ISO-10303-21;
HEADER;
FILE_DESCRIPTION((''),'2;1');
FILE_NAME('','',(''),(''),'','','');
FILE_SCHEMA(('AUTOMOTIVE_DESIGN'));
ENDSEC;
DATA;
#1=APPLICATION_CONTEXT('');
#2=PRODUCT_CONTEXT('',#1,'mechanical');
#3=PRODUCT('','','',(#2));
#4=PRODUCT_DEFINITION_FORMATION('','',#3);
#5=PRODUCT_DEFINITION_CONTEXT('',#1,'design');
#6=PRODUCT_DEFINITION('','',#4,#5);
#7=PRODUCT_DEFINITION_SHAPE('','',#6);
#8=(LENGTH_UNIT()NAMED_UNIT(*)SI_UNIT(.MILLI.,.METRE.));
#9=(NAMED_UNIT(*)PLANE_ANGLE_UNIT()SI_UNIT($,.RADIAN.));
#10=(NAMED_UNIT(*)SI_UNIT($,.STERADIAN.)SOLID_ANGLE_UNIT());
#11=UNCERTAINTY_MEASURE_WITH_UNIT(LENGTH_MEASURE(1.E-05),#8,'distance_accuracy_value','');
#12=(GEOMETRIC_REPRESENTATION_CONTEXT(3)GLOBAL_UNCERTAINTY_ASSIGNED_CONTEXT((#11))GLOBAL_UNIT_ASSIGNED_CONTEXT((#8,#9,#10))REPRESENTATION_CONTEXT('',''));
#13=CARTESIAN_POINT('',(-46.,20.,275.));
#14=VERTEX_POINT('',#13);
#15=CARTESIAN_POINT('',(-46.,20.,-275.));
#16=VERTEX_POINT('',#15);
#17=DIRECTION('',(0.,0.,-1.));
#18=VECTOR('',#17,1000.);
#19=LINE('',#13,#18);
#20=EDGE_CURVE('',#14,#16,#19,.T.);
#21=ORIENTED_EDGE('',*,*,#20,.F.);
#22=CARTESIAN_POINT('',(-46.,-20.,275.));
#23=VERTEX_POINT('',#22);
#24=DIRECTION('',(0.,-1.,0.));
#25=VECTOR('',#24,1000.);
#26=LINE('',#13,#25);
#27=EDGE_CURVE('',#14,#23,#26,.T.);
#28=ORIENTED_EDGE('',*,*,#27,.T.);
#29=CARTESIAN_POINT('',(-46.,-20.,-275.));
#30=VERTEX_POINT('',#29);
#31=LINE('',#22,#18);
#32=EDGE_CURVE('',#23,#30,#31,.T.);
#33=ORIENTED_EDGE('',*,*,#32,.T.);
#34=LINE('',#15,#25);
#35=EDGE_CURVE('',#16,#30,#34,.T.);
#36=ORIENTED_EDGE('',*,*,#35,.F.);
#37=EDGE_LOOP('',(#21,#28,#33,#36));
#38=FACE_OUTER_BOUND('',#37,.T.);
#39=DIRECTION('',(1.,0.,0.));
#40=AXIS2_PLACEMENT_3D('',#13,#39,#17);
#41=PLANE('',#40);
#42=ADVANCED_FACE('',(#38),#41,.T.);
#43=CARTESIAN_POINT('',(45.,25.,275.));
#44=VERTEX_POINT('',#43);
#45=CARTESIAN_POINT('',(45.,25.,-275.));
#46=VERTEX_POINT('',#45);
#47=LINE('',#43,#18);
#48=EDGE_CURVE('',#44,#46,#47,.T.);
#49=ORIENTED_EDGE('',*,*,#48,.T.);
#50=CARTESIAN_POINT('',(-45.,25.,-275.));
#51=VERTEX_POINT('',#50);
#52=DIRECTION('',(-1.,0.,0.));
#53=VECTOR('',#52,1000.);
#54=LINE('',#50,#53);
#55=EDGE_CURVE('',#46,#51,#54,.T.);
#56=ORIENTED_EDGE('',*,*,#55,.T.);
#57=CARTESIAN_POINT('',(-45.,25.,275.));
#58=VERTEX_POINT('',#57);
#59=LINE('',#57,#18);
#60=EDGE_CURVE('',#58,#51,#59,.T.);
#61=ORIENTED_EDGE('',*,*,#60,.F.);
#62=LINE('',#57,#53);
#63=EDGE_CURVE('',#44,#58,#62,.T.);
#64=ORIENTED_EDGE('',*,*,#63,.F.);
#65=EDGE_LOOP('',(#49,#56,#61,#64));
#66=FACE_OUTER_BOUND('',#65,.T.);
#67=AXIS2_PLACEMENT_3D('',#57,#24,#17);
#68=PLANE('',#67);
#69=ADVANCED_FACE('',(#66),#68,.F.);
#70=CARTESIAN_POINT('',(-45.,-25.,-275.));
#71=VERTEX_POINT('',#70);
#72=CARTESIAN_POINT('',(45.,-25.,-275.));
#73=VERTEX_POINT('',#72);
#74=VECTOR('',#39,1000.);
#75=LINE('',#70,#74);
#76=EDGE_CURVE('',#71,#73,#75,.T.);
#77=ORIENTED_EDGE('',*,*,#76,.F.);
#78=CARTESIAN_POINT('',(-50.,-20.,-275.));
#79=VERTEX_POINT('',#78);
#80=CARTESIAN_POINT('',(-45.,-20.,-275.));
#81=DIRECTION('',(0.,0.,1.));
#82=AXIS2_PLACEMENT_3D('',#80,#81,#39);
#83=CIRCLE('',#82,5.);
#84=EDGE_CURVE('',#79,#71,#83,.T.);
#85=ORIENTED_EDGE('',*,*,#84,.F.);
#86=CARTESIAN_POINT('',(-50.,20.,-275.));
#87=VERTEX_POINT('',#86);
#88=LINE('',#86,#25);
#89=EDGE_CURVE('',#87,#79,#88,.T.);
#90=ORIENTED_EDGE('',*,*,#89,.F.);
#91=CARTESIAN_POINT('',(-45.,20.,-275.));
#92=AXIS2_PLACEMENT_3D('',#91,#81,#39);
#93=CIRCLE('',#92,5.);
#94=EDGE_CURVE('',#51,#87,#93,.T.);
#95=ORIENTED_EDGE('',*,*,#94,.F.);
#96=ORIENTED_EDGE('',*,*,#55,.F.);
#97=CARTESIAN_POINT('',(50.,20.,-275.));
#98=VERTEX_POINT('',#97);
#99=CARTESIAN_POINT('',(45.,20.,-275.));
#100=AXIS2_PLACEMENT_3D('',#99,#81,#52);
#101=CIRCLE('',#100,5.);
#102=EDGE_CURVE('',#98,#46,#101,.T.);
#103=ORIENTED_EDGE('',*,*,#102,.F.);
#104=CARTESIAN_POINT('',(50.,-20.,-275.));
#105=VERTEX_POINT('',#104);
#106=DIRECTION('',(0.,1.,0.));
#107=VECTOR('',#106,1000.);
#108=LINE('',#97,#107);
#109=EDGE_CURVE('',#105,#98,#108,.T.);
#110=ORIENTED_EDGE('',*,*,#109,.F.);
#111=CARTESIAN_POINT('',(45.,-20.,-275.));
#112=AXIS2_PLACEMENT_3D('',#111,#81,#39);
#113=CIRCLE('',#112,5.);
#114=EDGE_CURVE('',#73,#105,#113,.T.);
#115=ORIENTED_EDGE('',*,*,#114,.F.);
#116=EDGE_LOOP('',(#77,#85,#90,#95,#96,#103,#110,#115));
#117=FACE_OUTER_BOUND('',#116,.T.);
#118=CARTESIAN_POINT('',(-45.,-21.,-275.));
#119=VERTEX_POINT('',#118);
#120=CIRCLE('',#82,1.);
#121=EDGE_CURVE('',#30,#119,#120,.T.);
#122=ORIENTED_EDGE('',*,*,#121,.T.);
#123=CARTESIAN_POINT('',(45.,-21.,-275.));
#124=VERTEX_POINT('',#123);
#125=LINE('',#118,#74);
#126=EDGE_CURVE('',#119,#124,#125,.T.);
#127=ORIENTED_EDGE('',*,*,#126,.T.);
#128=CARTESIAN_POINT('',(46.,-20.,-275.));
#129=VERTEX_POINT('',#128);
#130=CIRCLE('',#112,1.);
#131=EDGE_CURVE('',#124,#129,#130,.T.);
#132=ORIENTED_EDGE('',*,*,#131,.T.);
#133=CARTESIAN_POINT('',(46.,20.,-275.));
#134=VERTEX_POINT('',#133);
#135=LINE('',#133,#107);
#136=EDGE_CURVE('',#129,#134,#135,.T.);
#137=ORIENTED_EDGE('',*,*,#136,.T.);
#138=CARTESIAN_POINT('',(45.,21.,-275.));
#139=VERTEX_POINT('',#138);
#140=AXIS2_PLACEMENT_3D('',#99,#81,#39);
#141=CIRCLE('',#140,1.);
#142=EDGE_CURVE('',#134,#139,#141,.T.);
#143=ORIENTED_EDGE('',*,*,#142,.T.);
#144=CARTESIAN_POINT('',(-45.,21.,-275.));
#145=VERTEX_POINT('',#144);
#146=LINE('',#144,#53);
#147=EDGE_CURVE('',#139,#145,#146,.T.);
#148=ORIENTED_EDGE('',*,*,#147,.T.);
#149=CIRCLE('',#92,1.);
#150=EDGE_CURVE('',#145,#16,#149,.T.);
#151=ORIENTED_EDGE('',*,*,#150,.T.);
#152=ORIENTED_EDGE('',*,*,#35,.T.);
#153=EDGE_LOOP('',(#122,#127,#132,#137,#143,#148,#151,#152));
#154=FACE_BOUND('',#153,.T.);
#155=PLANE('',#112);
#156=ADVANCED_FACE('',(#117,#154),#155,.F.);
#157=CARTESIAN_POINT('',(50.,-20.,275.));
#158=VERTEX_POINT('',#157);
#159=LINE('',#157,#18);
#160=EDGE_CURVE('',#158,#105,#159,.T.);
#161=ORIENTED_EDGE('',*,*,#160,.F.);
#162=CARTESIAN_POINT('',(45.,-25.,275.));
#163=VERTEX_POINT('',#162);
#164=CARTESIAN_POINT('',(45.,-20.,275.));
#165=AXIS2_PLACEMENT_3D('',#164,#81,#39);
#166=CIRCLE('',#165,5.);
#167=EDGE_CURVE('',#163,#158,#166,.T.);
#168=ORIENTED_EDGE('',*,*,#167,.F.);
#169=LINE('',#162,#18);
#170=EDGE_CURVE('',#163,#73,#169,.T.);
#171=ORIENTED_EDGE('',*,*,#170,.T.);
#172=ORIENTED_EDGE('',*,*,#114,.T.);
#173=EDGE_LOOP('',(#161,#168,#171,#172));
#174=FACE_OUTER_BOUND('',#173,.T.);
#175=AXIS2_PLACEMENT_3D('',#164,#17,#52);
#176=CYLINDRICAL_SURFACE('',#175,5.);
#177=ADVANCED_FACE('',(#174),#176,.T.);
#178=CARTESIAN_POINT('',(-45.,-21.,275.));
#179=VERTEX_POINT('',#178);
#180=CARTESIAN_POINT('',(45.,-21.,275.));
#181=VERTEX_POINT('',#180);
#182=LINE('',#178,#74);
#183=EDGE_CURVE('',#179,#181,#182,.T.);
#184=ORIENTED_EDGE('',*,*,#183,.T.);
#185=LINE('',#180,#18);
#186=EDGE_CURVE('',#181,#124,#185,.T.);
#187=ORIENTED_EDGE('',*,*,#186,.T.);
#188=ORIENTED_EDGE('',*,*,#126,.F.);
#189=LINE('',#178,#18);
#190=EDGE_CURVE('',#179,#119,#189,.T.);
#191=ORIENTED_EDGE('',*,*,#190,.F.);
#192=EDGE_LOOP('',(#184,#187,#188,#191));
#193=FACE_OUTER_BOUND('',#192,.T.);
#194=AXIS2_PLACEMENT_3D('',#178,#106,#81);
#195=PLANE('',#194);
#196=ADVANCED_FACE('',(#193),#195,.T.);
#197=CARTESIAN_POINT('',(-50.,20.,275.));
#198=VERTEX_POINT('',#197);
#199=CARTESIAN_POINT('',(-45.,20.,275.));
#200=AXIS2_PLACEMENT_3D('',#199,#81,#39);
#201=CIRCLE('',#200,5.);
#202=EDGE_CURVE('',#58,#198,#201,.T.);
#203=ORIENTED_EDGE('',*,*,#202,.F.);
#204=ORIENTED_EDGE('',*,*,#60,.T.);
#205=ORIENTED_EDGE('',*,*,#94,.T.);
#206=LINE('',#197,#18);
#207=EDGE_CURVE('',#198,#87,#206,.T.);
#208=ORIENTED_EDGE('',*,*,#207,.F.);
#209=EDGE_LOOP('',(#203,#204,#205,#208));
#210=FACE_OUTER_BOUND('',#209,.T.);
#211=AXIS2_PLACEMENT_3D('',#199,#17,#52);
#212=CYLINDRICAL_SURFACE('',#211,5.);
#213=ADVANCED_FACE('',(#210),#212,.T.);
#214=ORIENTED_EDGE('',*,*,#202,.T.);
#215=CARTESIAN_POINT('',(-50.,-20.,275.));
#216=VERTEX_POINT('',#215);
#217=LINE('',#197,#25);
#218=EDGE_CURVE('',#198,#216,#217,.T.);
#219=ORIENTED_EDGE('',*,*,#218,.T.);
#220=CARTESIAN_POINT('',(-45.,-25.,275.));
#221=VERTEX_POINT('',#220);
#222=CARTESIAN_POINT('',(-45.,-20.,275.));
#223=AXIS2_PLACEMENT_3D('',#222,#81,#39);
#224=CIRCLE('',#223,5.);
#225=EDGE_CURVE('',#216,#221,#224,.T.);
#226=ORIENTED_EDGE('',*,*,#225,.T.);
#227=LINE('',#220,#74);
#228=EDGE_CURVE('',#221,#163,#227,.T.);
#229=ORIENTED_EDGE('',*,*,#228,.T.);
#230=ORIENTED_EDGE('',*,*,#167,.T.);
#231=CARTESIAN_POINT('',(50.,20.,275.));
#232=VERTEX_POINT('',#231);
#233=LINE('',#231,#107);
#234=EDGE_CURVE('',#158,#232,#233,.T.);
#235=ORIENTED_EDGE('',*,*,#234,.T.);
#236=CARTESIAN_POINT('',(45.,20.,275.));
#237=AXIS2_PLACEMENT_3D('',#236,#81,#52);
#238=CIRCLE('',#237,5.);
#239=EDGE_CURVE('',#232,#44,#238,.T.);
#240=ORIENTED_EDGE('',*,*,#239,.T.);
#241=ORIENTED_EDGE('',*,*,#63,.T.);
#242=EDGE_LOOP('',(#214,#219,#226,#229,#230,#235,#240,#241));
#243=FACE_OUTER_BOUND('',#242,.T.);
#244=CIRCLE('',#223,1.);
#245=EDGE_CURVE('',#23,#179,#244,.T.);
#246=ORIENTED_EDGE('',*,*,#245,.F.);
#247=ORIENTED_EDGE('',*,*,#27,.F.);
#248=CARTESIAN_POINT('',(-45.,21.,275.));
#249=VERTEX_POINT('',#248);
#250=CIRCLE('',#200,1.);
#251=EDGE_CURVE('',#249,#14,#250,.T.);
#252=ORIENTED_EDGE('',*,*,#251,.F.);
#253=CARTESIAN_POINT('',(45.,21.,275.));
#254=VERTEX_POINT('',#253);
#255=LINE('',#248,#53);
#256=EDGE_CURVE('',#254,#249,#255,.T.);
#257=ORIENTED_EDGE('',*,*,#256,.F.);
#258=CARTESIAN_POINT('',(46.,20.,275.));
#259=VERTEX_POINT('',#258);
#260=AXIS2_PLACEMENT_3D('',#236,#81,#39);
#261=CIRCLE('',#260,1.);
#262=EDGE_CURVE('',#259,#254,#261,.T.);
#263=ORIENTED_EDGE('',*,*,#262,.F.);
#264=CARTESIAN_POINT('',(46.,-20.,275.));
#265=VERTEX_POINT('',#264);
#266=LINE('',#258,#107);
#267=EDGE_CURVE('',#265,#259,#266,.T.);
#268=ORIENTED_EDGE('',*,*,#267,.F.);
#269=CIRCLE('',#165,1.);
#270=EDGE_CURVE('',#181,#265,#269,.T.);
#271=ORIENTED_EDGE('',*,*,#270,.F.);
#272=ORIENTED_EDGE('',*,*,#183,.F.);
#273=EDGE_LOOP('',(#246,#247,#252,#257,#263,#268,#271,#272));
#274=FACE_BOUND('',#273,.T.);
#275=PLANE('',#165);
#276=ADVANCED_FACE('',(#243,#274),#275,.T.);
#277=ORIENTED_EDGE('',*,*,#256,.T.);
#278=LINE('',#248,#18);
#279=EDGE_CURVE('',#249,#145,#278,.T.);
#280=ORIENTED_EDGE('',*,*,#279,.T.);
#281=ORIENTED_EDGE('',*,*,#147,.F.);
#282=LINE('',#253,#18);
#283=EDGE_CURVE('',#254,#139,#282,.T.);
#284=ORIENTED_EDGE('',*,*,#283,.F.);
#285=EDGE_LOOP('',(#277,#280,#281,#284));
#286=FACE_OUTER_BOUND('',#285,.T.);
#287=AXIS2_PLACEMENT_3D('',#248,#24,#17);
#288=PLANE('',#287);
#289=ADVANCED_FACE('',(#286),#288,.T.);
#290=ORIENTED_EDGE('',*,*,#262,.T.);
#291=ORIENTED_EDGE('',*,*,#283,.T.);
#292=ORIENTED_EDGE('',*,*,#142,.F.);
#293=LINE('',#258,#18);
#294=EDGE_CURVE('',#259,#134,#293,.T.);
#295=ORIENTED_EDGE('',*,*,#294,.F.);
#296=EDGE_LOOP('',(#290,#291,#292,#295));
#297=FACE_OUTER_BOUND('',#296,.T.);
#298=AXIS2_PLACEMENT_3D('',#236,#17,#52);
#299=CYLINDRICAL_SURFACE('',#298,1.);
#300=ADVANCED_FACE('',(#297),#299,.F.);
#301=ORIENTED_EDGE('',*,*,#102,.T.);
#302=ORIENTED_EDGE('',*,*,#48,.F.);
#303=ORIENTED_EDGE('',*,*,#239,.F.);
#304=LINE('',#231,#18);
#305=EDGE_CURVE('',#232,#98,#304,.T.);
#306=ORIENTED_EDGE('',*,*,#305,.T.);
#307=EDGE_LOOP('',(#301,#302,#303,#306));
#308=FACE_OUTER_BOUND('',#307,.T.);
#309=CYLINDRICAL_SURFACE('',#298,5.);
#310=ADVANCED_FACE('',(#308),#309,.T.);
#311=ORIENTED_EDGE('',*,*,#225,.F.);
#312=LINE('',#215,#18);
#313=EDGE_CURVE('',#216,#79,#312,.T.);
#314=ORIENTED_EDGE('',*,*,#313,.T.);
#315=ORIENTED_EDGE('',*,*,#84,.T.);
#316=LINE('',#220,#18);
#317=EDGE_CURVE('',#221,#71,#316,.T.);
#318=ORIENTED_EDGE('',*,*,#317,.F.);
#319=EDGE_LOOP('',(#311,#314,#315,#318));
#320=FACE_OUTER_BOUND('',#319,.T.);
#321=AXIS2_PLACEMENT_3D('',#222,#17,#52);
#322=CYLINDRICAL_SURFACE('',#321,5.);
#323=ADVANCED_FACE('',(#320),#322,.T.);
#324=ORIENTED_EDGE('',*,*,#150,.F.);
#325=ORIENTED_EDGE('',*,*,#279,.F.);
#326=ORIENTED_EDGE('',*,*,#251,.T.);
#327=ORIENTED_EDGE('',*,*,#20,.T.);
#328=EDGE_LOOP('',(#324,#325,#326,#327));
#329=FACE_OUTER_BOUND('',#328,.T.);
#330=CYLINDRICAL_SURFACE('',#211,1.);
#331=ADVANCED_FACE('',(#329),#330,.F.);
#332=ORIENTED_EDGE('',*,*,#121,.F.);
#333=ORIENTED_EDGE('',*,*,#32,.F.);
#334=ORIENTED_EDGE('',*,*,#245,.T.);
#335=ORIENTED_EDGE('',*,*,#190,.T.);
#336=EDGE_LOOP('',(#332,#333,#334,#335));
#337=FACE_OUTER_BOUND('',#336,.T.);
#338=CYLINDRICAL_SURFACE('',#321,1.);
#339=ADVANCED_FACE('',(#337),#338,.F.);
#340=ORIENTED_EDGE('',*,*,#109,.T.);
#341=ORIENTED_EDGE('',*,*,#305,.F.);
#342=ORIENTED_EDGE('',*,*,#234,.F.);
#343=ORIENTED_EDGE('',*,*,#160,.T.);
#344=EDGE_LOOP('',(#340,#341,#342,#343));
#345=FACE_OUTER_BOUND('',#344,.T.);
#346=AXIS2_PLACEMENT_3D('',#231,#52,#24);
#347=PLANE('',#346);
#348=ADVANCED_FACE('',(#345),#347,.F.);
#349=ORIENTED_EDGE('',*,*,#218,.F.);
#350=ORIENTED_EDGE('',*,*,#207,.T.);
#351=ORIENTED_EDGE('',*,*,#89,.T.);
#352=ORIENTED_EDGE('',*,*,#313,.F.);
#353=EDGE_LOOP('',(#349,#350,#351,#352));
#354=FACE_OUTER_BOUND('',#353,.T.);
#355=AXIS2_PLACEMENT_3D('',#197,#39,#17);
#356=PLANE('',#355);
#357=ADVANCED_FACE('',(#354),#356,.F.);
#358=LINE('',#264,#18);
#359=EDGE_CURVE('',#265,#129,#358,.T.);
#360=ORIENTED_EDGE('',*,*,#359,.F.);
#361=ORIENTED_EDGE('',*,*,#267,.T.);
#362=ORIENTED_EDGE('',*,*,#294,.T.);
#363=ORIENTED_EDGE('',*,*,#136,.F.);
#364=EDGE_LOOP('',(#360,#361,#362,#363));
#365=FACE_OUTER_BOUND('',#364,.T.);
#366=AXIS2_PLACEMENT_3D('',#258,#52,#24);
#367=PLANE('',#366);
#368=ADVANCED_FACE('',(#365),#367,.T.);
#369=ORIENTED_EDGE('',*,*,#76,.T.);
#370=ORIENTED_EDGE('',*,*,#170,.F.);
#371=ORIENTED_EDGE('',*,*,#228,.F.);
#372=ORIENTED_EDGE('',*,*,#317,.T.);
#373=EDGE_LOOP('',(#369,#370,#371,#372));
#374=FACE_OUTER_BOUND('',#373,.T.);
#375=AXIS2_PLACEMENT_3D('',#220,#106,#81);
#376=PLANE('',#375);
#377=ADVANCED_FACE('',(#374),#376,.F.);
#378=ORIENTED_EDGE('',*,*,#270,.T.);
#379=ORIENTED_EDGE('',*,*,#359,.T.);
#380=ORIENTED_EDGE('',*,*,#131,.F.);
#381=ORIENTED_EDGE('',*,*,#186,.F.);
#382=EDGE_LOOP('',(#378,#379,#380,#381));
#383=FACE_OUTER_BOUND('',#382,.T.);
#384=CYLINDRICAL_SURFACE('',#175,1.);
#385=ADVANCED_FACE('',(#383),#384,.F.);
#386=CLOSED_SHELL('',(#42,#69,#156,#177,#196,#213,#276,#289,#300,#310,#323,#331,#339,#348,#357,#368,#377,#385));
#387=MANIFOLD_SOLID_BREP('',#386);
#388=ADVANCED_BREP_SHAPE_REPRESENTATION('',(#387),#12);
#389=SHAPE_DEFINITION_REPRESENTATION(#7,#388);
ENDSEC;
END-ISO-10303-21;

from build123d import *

# Parameters (mm, degrees)
EXTRUDE_1_DEPTH = 275


with BuildPart() as part:
    # 草图1 → 拉伸-薄壁1 (new, symmetric)
    with BuildSketch(Plane.XY):
        with BuildLine():
            Line((-45, 25), (45, 25))
            ThreePointArc((45, 25), (48.535533906, 23.535533906), (50, 20))
            Line((50, 20), (50, -20))
            ThreePointArc((50, -20), (48.535533906, -23.535533906), (45, -25))
            Line((45, -25), (-45, -25))
            ThreePointArc((-45, -25), (-48.535533906, -23.535533906), (-50, -20))
            Line((-50, -20), (-50, 20))
            ThreePointArc((-50, 20), (-48.535533906, 23.535533906), (-45, 25))
        make_face()
        with BuildLine():
            Line((-45, 21), (45, 21))
            ThreePointArc((45, 21), (45.707106781, 20.707106781), (46, 20))
            Line((46, 20), (46, -20))
            ThreePointArc((46, -20), (45.707106781, -20.707106781), (45, -21))
            Line((45, -21), (-45, -21))
            ThreePointArc((-45, -21), (-45.707106781, -20.707106781), (-46, -20))
            Line((-46, -20), (-46, 20))
            ThreePointArc((-46, 20), (-45.707106781, 20.707106781), (-45, 21))
        make_face(mode=Mode.SUBTRACT)
    extrude(amount=EXTRUDE_1_DEPTH, both=True)


solid = part.part
